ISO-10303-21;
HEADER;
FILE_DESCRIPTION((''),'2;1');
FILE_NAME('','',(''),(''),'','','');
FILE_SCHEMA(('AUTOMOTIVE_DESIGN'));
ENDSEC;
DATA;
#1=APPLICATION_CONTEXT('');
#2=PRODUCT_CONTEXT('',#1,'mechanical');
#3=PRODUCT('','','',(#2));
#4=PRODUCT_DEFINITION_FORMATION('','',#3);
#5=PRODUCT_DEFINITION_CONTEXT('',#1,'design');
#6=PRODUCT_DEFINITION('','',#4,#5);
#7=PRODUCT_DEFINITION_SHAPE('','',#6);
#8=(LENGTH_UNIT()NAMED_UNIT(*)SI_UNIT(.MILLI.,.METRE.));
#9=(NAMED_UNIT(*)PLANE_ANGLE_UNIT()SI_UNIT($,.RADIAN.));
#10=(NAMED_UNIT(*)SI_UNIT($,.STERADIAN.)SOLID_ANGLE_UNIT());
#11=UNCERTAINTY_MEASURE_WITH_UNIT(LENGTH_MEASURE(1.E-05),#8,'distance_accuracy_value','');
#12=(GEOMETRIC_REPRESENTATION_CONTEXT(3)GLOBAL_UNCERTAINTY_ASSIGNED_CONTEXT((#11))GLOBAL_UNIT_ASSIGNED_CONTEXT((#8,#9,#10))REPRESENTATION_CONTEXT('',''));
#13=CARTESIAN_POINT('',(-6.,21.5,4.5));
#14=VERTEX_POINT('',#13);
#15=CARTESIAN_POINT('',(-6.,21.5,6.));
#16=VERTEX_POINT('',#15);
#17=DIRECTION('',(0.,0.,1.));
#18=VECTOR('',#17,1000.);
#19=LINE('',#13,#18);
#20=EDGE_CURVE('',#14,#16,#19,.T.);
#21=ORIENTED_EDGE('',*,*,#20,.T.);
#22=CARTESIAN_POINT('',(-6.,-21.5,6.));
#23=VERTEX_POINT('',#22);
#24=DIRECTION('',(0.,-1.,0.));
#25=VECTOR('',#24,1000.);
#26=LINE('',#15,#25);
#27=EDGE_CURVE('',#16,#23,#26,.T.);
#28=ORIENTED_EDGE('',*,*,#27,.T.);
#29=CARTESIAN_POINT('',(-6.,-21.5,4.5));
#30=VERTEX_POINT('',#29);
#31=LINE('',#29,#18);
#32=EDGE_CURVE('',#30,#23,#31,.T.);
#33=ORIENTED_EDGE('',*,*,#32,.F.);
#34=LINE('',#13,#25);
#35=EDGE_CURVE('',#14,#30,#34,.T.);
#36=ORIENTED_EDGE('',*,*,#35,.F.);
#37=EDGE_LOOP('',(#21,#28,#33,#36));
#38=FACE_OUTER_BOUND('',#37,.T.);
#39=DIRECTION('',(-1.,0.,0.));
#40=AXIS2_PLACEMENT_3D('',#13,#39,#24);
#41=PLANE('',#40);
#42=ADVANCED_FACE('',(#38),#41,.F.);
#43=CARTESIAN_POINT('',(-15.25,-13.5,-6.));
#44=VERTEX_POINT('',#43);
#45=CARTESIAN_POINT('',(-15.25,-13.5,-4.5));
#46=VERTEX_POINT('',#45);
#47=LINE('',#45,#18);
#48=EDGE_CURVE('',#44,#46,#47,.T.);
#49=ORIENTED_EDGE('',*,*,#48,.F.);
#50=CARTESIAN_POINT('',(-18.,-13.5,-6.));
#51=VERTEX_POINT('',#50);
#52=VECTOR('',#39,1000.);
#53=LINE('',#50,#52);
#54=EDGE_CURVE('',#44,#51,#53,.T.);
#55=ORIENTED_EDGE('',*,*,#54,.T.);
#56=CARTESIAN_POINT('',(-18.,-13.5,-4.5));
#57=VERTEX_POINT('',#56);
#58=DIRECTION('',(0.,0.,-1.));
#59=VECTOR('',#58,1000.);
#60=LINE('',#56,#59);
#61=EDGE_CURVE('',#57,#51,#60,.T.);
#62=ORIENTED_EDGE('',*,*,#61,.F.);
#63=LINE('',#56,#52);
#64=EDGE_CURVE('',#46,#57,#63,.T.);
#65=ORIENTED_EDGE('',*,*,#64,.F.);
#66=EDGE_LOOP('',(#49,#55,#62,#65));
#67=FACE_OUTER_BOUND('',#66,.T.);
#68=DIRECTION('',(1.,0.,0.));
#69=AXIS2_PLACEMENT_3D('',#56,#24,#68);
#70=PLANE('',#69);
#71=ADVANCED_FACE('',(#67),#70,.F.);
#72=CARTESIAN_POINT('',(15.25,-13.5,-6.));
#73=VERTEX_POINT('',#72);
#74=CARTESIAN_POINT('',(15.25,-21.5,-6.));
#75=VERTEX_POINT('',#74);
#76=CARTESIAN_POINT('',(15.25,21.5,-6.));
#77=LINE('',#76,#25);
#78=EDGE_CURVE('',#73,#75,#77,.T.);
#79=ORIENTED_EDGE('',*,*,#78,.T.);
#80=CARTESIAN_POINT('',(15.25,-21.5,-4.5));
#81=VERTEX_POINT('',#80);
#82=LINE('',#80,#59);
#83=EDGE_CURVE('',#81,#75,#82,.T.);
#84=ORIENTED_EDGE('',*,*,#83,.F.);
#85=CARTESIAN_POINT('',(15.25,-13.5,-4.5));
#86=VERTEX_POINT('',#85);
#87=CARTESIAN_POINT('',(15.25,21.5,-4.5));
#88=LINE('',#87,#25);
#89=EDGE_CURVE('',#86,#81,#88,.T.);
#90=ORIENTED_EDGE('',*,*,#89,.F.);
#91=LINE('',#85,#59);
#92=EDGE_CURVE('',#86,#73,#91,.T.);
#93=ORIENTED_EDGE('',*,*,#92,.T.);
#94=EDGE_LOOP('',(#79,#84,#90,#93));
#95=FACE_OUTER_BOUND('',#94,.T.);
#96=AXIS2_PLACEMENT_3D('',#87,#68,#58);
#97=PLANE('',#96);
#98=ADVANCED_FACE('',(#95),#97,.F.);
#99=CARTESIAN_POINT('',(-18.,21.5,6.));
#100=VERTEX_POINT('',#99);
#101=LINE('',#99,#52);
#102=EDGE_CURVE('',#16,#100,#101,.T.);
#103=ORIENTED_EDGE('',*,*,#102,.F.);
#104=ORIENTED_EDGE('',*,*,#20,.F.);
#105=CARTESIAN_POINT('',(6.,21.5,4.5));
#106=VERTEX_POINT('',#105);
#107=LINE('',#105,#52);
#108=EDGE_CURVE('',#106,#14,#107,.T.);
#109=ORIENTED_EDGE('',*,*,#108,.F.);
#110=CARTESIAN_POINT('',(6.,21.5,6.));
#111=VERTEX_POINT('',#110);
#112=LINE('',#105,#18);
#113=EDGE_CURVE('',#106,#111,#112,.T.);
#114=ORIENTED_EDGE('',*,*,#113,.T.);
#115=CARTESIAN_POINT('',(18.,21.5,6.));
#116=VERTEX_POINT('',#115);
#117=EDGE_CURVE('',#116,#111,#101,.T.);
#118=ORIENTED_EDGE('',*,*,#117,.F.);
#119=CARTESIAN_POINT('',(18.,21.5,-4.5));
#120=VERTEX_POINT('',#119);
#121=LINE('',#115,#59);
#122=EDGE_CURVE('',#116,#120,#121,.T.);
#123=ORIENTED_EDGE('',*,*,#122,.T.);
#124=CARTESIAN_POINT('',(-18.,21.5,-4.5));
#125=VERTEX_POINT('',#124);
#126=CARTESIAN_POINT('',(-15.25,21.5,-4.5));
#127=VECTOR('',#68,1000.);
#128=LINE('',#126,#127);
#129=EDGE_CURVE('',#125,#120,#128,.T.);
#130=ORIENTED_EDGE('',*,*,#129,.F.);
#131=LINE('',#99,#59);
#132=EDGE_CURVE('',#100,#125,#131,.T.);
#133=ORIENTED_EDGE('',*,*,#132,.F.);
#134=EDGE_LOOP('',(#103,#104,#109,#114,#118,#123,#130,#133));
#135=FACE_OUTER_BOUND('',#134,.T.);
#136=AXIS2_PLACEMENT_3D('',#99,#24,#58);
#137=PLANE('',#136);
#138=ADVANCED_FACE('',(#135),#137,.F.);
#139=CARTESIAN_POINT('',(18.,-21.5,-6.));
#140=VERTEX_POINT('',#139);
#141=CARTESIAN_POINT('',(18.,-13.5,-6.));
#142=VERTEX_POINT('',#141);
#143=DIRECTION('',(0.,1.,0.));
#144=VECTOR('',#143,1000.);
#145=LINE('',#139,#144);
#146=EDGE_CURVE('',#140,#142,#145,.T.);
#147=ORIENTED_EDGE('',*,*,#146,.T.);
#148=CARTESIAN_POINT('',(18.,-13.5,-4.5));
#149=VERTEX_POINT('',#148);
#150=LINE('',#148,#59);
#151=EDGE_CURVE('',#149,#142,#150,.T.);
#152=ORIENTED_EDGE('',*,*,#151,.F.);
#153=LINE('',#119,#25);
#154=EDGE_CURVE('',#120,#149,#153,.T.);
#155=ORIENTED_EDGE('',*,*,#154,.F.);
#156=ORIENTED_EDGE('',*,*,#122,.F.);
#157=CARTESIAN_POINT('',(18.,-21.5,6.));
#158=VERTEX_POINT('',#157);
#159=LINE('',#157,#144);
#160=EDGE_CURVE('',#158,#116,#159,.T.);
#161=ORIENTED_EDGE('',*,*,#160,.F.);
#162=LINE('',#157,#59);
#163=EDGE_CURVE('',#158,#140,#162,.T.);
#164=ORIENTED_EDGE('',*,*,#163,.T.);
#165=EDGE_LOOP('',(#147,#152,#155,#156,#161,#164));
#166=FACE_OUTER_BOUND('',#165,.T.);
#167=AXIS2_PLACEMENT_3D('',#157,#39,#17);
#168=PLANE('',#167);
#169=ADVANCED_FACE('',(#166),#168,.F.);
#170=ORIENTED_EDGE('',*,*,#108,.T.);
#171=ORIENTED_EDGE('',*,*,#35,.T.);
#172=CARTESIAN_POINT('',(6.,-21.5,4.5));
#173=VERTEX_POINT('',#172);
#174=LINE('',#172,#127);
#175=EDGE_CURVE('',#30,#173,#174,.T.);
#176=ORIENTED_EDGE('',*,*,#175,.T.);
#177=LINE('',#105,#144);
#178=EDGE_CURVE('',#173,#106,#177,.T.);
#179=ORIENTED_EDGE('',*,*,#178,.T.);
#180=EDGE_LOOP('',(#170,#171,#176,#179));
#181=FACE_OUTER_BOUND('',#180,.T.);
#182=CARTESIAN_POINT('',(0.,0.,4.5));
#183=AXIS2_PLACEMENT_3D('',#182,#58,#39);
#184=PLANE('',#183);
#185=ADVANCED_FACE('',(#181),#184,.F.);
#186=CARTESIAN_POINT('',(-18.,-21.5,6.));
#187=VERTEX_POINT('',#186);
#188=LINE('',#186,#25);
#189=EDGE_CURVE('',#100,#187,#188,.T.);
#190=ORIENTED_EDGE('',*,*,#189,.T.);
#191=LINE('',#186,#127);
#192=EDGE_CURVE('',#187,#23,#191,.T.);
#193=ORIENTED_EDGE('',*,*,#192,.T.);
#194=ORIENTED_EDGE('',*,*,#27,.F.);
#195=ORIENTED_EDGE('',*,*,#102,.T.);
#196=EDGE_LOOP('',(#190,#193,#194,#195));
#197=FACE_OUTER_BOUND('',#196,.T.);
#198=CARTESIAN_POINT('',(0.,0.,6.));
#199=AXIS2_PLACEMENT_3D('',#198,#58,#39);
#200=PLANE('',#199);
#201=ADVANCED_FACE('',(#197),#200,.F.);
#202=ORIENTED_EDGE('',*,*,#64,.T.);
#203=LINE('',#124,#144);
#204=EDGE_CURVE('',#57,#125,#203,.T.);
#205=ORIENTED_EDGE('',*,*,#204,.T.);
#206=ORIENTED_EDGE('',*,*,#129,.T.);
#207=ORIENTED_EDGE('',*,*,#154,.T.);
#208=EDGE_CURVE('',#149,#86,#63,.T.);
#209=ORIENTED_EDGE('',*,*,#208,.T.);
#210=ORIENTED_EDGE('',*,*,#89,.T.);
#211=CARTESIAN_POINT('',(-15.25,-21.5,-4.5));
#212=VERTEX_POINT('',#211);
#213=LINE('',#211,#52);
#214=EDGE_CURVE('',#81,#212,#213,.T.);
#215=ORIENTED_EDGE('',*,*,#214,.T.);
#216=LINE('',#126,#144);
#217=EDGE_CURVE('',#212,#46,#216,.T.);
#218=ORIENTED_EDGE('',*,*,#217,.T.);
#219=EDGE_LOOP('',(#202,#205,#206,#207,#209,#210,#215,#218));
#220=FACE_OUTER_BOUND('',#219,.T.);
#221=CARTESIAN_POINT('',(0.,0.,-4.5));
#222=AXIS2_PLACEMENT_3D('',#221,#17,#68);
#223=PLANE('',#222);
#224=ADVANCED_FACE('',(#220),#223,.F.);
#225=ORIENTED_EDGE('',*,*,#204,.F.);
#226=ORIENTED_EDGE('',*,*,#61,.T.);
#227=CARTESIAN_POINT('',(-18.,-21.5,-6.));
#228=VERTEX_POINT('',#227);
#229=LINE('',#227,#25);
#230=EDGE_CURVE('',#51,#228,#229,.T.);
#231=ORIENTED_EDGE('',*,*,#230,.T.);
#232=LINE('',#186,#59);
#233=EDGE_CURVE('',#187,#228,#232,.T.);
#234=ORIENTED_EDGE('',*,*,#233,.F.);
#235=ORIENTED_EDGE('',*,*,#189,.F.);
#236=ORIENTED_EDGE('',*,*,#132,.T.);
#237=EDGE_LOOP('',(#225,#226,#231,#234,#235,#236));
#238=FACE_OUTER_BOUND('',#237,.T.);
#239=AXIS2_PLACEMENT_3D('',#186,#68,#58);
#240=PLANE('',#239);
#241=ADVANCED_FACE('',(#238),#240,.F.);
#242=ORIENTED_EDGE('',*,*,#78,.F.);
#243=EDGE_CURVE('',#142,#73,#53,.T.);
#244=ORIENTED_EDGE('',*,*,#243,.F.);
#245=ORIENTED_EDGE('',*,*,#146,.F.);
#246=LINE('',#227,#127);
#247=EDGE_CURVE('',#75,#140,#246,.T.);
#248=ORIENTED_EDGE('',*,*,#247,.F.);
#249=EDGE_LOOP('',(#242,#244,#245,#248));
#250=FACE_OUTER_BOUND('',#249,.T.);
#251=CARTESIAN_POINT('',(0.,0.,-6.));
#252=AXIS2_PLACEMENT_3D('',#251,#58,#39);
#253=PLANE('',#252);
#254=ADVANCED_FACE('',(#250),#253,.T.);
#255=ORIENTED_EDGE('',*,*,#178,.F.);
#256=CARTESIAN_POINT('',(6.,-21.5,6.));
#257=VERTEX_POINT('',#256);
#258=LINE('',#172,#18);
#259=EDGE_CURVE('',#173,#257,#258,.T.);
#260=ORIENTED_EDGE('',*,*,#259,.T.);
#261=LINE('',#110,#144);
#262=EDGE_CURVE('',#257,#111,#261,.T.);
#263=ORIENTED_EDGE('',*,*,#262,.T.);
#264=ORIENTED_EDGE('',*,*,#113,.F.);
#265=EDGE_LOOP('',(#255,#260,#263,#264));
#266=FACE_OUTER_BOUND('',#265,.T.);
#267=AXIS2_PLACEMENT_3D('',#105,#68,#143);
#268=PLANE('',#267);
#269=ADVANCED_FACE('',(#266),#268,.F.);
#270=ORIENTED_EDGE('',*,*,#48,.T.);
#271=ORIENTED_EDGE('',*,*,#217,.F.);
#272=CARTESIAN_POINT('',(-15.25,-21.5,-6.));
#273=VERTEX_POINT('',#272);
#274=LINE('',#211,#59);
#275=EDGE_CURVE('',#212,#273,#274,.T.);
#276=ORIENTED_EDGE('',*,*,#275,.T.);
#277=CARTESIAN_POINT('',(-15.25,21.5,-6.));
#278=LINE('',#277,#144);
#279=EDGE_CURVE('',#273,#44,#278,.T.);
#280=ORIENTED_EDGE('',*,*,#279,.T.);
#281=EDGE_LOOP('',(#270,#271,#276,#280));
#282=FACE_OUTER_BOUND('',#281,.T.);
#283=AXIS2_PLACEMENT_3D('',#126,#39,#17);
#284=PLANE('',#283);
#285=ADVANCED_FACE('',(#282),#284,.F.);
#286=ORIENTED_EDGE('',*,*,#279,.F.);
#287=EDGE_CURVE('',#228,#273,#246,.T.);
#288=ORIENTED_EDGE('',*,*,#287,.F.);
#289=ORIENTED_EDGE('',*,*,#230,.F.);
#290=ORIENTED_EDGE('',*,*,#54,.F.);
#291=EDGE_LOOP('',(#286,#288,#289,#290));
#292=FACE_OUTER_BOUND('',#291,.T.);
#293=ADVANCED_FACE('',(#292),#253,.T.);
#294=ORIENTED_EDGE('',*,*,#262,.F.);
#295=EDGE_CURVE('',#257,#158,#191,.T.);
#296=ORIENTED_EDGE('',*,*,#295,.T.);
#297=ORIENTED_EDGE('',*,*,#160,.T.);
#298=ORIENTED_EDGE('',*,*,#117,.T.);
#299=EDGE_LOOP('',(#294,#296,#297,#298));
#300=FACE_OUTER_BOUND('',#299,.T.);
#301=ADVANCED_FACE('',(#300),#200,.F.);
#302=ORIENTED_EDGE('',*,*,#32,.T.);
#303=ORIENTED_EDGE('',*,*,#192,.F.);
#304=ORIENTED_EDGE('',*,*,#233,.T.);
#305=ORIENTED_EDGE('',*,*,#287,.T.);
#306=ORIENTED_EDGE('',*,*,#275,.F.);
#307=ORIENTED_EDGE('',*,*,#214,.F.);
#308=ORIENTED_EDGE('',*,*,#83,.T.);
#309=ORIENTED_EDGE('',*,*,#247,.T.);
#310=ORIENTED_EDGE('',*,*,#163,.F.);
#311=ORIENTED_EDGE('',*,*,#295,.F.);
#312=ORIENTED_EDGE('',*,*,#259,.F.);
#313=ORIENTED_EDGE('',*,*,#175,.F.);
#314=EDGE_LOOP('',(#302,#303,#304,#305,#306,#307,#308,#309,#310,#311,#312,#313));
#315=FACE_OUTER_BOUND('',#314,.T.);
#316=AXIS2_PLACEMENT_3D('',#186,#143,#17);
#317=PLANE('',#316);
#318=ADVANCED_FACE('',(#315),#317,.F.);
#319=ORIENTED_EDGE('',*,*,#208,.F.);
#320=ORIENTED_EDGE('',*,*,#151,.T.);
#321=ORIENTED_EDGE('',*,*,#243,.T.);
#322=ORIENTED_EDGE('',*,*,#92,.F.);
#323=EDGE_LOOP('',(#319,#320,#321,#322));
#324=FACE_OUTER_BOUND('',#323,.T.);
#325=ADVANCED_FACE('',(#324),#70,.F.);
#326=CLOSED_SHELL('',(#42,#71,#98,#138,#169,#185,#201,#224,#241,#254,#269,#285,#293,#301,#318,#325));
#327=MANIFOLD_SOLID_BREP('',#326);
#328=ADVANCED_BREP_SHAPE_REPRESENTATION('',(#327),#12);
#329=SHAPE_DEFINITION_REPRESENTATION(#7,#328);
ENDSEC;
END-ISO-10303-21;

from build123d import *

# Parameters (mm, degrees)
SKETCH_1_W          = 36
SKETCH_1_H          = 43
EXTRUDE_1_DEPTH     = 6
SKETCH_2_W          = 12
SKETCH_2_H          = 43
CUT_EXTRUDE_1_DEPTH = 1.5
SKETCH_3_W          = 30.5
SKETCH_3_H          = 43
CUT_EXTRUDE_2_DEPTH = 1.5
SKETCH_4_W          = 36
SKETCH_4_H          = 35
CUT_EXTRUDE_3_DEPTH = 1.5


with BuildPart() as part:
    # 草图1 → 凸台-拉伸1 (new, symmetric)
    with BuildSketch(Plane.XY):
        Rectangle(SKETCH_1_W, SKETCH_1_H)
    extrude(amount=EXTRUDE_1_DEPTH, both=True)

    # 草图2 → 切除-拉伸1 (cut)
    with BuildSketch(Plane.XY.offset(6)):
        Rectangle(SKETCH_2_W, SKETCH_2_H)
    extrude(amount=-CUT_EXTRUDE_1_DEPTH, mode=Mode.SUBTRACT)

    # 草图3 → 切除-拉伸2 (cut)
    with BuildSketch(Plane(origin=(0, 0, -6), x_dir=(-1, 0, 0), z_dir=(0, 0, -1))):
        Rectangle(SKETCH_3_W, SKETCH_3_H)
    extrude(amount=-CUT_EXTRUDE_2_DEPTH, mode=Mode.SUBTRACT)

    # 草图4 → 切除-拉伸3 (cut)
    with BuildSketch(Plane(origin=(0, 0, -6), x_dir=(-1, 0, 0), z_dir=(0, 0, -1))):
        with Locations((0, 4)):
            Rectangle(SKETCH_4_W, SKETCH_4_H)
    extrude(amount=-CUT_EXTRUDE_3_DEPTH, mode=Mode.SUBTRACT)


solid = part.part
